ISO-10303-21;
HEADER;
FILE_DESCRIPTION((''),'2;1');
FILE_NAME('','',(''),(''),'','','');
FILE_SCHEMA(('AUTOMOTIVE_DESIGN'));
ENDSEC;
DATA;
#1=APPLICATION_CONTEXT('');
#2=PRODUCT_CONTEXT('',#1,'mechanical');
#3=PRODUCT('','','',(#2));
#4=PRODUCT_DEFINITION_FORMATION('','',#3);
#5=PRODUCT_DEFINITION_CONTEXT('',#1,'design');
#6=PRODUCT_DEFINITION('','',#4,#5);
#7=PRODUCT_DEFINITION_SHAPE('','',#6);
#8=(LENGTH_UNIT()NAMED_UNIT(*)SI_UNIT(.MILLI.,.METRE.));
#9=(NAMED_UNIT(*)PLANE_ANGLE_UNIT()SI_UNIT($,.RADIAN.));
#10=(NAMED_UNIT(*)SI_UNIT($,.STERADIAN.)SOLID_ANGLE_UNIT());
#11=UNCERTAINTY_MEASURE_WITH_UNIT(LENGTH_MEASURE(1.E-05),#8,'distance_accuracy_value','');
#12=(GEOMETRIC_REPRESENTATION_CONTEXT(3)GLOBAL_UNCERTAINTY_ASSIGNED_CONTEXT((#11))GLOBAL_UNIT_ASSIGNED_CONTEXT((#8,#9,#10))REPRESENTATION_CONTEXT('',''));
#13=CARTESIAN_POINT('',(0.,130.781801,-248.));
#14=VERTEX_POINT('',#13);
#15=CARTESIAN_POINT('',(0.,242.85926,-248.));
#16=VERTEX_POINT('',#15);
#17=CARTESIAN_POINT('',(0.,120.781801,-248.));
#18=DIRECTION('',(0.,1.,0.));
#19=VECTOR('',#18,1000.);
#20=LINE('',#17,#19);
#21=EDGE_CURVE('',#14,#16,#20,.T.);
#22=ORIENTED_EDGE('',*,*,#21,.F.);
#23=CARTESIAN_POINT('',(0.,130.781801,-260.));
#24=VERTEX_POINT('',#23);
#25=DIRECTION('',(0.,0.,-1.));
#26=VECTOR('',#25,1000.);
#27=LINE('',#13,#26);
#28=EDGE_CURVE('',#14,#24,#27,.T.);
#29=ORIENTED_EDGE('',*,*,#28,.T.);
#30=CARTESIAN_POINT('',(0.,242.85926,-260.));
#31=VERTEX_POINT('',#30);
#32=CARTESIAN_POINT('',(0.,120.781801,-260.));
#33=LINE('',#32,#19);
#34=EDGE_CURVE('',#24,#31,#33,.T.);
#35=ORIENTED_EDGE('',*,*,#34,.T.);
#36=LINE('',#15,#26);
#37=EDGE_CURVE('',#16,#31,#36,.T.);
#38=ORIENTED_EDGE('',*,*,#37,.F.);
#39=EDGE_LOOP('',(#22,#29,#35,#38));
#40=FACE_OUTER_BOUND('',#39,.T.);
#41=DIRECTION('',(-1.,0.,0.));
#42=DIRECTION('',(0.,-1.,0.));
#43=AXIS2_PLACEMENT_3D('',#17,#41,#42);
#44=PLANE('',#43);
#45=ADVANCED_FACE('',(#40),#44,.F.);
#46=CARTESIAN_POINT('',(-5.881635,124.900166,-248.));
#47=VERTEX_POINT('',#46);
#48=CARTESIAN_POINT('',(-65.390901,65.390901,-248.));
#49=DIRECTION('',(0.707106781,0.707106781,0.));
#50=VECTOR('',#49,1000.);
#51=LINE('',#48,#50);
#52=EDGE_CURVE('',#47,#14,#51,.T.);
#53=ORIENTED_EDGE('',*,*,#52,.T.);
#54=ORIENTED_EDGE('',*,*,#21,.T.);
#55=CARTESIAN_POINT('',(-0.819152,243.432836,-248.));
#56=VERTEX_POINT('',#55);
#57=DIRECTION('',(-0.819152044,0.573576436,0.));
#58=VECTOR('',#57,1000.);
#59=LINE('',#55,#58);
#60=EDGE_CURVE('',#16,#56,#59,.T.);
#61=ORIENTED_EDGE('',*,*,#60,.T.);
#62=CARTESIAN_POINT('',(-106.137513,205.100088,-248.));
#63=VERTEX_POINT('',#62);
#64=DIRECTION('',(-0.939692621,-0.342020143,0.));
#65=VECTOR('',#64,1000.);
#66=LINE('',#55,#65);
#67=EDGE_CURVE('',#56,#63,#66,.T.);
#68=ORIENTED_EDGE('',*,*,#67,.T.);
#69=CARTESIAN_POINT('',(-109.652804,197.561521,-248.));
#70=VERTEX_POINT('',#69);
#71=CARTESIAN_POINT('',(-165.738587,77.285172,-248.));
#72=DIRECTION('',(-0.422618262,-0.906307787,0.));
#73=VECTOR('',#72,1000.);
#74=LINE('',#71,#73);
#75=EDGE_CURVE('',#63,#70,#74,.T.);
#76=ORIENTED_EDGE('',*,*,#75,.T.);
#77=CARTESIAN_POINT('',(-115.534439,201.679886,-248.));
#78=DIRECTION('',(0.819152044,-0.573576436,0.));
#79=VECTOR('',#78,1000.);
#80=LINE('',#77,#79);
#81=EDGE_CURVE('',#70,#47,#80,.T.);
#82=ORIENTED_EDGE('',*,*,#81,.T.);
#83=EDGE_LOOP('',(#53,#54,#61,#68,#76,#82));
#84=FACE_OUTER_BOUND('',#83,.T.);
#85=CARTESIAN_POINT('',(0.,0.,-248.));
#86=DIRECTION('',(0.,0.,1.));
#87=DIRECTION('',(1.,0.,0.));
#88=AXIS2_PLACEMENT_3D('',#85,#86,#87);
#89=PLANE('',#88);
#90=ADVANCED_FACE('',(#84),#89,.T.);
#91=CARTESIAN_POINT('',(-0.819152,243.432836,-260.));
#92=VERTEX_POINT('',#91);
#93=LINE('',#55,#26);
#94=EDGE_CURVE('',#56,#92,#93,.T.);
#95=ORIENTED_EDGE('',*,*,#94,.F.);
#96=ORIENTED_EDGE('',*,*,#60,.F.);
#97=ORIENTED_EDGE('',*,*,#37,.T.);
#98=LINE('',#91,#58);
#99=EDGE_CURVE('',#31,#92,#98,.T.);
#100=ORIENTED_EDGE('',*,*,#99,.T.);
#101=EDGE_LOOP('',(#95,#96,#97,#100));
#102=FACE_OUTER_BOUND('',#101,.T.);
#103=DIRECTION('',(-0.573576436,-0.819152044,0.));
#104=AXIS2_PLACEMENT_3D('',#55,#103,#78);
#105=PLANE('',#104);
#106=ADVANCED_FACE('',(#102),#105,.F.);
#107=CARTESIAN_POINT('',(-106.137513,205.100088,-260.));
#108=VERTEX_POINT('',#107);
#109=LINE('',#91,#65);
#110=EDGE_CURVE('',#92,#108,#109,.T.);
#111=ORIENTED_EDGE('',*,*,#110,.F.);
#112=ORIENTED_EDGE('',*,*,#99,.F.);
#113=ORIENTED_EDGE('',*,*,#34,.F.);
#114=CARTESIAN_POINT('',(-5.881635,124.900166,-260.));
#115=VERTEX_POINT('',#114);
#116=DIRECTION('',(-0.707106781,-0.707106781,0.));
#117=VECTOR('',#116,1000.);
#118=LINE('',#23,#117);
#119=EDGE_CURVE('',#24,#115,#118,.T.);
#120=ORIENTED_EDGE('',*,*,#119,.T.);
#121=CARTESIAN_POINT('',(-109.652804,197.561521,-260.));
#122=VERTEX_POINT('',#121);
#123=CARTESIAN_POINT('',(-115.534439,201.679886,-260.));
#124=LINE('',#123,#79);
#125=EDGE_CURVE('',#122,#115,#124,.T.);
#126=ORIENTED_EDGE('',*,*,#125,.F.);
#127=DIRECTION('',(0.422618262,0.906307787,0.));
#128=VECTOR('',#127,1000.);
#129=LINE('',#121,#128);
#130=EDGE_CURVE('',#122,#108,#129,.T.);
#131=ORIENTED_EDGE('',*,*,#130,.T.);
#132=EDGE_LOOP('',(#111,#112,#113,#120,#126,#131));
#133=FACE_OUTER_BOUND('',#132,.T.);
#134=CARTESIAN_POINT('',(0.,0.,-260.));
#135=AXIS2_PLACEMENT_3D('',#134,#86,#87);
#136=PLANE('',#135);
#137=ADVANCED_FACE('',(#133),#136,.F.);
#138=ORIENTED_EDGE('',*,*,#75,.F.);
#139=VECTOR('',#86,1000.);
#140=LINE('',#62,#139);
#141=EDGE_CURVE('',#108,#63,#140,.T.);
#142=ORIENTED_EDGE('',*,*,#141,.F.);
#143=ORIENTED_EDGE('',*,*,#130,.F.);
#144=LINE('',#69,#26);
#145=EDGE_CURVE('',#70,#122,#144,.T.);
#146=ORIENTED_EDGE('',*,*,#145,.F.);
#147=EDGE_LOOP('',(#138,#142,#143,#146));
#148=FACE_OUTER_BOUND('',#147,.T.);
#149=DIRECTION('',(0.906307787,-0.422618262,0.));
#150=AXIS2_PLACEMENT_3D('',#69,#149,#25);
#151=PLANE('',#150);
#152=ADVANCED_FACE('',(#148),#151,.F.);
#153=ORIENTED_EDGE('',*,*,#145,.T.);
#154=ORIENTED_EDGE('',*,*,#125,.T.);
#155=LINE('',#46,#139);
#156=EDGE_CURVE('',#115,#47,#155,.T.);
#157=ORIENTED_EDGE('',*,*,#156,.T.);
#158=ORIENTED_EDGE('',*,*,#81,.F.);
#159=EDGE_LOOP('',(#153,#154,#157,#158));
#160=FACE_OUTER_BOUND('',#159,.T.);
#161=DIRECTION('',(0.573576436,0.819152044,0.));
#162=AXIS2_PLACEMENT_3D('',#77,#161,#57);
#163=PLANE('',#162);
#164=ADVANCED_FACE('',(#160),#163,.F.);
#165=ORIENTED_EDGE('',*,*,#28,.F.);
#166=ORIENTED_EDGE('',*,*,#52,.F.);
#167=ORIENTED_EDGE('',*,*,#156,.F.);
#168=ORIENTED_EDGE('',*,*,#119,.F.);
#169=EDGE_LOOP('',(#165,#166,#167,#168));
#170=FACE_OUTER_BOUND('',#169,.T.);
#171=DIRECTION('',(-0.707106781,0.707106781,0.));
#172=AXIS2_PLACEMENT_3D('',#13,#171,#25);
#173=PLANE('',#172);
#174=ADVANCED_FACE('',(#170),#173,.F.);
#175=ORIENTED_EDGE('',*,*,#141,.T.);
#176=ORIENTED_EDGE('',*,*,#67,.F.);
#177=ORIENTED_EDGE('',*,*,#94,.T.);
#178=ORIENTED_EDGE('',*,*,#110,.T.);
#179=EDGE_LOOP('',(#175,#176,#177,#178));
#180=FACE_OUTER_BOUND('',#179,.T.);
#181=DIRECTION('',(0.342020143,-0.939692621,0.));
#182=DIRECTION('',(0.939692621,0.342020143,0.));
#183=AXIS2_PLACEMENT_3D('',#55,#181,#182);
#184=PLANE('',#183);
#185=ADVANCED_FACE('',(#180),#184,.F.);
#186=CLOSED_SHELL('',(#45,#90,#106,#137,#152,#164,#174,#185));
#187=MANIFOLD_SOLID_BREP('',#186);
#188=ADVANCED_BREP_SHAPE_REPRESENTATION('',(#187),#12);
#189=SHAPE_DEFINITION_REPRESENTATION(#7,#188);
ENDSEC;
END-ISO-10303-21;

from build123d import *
from OCP.BRepFilletAPI import BRepFilletAPI_MakeChamfer

# Parameters (mm, degrees)
EXTRUDE_START   = -260
EXTRUDE_1_DEPTH = 12
CHAMFER_1_SIZE  = 10
CHAMFER_1_SIZE2 = 7.180150431


with BuildPart() as part:
    # 草图1 → 凸台-拉伸1 (new body)
    with BuildSketch(Plane.XY.offset(EXTRUDE_START)):
        Polygon((-0.819152044, 243.432836403), (-115.534439314, 201.679886421), (0, 120.78180109), (0, 242.859259966), align=None)
    extrude(amount=EXTRUDE_1_DEPTH)

    # 倒角1: one chamfer whose edges measure the first distance from different faces: ONE call of the kernel's chamfer builder (chamfer() names one face for all edges)
    chamfer_1_edges_1 = [part.edges().sort_by_distance(p)[0] for p in [
        (0, 120.78180109, -254),
    ]]
    chamfer_1_side_1 = [part.faces().sort_by_distance(p)[0] for p in [
        (0, 181.820530528, -254),
    ]]
    chamfer_1_edges_2 = [part.edges().sort_by_distance(p)[0] for p in [
        (-115.534439314, 201.679886421, -254),
    ]]
    chamfer_1_side_2 = [part.faces().sort_by_distance(p)[0] for p in [
        (-58.176795679, 222.556361412, -254),
    ]]
    chamfer_1 = BRepFilletAPI_MakeChamfer(part.part.solid().wrapped)
    for e in chamfer_1_edges_1:
        chamfer_1.Add(CHAMFER_1_SIZE, CHAMFER_1_SIZE2, e.wrapped, chamfer_1_side_1[0].wrapped)  # the first distance lies on this face
    for e in chamfer_1_edges_2:
        chamfer_1.Add(CHAMFER_1_SIZE, CHAMFER_1_SIZE2, e.wrapped, chamfer_1_side_2[0].wrapped)  # the first distance lies on this face
    add(Compound.cast(chamfer_1.Shape()), mode=Mode.REPLACE)


solid = part.part
